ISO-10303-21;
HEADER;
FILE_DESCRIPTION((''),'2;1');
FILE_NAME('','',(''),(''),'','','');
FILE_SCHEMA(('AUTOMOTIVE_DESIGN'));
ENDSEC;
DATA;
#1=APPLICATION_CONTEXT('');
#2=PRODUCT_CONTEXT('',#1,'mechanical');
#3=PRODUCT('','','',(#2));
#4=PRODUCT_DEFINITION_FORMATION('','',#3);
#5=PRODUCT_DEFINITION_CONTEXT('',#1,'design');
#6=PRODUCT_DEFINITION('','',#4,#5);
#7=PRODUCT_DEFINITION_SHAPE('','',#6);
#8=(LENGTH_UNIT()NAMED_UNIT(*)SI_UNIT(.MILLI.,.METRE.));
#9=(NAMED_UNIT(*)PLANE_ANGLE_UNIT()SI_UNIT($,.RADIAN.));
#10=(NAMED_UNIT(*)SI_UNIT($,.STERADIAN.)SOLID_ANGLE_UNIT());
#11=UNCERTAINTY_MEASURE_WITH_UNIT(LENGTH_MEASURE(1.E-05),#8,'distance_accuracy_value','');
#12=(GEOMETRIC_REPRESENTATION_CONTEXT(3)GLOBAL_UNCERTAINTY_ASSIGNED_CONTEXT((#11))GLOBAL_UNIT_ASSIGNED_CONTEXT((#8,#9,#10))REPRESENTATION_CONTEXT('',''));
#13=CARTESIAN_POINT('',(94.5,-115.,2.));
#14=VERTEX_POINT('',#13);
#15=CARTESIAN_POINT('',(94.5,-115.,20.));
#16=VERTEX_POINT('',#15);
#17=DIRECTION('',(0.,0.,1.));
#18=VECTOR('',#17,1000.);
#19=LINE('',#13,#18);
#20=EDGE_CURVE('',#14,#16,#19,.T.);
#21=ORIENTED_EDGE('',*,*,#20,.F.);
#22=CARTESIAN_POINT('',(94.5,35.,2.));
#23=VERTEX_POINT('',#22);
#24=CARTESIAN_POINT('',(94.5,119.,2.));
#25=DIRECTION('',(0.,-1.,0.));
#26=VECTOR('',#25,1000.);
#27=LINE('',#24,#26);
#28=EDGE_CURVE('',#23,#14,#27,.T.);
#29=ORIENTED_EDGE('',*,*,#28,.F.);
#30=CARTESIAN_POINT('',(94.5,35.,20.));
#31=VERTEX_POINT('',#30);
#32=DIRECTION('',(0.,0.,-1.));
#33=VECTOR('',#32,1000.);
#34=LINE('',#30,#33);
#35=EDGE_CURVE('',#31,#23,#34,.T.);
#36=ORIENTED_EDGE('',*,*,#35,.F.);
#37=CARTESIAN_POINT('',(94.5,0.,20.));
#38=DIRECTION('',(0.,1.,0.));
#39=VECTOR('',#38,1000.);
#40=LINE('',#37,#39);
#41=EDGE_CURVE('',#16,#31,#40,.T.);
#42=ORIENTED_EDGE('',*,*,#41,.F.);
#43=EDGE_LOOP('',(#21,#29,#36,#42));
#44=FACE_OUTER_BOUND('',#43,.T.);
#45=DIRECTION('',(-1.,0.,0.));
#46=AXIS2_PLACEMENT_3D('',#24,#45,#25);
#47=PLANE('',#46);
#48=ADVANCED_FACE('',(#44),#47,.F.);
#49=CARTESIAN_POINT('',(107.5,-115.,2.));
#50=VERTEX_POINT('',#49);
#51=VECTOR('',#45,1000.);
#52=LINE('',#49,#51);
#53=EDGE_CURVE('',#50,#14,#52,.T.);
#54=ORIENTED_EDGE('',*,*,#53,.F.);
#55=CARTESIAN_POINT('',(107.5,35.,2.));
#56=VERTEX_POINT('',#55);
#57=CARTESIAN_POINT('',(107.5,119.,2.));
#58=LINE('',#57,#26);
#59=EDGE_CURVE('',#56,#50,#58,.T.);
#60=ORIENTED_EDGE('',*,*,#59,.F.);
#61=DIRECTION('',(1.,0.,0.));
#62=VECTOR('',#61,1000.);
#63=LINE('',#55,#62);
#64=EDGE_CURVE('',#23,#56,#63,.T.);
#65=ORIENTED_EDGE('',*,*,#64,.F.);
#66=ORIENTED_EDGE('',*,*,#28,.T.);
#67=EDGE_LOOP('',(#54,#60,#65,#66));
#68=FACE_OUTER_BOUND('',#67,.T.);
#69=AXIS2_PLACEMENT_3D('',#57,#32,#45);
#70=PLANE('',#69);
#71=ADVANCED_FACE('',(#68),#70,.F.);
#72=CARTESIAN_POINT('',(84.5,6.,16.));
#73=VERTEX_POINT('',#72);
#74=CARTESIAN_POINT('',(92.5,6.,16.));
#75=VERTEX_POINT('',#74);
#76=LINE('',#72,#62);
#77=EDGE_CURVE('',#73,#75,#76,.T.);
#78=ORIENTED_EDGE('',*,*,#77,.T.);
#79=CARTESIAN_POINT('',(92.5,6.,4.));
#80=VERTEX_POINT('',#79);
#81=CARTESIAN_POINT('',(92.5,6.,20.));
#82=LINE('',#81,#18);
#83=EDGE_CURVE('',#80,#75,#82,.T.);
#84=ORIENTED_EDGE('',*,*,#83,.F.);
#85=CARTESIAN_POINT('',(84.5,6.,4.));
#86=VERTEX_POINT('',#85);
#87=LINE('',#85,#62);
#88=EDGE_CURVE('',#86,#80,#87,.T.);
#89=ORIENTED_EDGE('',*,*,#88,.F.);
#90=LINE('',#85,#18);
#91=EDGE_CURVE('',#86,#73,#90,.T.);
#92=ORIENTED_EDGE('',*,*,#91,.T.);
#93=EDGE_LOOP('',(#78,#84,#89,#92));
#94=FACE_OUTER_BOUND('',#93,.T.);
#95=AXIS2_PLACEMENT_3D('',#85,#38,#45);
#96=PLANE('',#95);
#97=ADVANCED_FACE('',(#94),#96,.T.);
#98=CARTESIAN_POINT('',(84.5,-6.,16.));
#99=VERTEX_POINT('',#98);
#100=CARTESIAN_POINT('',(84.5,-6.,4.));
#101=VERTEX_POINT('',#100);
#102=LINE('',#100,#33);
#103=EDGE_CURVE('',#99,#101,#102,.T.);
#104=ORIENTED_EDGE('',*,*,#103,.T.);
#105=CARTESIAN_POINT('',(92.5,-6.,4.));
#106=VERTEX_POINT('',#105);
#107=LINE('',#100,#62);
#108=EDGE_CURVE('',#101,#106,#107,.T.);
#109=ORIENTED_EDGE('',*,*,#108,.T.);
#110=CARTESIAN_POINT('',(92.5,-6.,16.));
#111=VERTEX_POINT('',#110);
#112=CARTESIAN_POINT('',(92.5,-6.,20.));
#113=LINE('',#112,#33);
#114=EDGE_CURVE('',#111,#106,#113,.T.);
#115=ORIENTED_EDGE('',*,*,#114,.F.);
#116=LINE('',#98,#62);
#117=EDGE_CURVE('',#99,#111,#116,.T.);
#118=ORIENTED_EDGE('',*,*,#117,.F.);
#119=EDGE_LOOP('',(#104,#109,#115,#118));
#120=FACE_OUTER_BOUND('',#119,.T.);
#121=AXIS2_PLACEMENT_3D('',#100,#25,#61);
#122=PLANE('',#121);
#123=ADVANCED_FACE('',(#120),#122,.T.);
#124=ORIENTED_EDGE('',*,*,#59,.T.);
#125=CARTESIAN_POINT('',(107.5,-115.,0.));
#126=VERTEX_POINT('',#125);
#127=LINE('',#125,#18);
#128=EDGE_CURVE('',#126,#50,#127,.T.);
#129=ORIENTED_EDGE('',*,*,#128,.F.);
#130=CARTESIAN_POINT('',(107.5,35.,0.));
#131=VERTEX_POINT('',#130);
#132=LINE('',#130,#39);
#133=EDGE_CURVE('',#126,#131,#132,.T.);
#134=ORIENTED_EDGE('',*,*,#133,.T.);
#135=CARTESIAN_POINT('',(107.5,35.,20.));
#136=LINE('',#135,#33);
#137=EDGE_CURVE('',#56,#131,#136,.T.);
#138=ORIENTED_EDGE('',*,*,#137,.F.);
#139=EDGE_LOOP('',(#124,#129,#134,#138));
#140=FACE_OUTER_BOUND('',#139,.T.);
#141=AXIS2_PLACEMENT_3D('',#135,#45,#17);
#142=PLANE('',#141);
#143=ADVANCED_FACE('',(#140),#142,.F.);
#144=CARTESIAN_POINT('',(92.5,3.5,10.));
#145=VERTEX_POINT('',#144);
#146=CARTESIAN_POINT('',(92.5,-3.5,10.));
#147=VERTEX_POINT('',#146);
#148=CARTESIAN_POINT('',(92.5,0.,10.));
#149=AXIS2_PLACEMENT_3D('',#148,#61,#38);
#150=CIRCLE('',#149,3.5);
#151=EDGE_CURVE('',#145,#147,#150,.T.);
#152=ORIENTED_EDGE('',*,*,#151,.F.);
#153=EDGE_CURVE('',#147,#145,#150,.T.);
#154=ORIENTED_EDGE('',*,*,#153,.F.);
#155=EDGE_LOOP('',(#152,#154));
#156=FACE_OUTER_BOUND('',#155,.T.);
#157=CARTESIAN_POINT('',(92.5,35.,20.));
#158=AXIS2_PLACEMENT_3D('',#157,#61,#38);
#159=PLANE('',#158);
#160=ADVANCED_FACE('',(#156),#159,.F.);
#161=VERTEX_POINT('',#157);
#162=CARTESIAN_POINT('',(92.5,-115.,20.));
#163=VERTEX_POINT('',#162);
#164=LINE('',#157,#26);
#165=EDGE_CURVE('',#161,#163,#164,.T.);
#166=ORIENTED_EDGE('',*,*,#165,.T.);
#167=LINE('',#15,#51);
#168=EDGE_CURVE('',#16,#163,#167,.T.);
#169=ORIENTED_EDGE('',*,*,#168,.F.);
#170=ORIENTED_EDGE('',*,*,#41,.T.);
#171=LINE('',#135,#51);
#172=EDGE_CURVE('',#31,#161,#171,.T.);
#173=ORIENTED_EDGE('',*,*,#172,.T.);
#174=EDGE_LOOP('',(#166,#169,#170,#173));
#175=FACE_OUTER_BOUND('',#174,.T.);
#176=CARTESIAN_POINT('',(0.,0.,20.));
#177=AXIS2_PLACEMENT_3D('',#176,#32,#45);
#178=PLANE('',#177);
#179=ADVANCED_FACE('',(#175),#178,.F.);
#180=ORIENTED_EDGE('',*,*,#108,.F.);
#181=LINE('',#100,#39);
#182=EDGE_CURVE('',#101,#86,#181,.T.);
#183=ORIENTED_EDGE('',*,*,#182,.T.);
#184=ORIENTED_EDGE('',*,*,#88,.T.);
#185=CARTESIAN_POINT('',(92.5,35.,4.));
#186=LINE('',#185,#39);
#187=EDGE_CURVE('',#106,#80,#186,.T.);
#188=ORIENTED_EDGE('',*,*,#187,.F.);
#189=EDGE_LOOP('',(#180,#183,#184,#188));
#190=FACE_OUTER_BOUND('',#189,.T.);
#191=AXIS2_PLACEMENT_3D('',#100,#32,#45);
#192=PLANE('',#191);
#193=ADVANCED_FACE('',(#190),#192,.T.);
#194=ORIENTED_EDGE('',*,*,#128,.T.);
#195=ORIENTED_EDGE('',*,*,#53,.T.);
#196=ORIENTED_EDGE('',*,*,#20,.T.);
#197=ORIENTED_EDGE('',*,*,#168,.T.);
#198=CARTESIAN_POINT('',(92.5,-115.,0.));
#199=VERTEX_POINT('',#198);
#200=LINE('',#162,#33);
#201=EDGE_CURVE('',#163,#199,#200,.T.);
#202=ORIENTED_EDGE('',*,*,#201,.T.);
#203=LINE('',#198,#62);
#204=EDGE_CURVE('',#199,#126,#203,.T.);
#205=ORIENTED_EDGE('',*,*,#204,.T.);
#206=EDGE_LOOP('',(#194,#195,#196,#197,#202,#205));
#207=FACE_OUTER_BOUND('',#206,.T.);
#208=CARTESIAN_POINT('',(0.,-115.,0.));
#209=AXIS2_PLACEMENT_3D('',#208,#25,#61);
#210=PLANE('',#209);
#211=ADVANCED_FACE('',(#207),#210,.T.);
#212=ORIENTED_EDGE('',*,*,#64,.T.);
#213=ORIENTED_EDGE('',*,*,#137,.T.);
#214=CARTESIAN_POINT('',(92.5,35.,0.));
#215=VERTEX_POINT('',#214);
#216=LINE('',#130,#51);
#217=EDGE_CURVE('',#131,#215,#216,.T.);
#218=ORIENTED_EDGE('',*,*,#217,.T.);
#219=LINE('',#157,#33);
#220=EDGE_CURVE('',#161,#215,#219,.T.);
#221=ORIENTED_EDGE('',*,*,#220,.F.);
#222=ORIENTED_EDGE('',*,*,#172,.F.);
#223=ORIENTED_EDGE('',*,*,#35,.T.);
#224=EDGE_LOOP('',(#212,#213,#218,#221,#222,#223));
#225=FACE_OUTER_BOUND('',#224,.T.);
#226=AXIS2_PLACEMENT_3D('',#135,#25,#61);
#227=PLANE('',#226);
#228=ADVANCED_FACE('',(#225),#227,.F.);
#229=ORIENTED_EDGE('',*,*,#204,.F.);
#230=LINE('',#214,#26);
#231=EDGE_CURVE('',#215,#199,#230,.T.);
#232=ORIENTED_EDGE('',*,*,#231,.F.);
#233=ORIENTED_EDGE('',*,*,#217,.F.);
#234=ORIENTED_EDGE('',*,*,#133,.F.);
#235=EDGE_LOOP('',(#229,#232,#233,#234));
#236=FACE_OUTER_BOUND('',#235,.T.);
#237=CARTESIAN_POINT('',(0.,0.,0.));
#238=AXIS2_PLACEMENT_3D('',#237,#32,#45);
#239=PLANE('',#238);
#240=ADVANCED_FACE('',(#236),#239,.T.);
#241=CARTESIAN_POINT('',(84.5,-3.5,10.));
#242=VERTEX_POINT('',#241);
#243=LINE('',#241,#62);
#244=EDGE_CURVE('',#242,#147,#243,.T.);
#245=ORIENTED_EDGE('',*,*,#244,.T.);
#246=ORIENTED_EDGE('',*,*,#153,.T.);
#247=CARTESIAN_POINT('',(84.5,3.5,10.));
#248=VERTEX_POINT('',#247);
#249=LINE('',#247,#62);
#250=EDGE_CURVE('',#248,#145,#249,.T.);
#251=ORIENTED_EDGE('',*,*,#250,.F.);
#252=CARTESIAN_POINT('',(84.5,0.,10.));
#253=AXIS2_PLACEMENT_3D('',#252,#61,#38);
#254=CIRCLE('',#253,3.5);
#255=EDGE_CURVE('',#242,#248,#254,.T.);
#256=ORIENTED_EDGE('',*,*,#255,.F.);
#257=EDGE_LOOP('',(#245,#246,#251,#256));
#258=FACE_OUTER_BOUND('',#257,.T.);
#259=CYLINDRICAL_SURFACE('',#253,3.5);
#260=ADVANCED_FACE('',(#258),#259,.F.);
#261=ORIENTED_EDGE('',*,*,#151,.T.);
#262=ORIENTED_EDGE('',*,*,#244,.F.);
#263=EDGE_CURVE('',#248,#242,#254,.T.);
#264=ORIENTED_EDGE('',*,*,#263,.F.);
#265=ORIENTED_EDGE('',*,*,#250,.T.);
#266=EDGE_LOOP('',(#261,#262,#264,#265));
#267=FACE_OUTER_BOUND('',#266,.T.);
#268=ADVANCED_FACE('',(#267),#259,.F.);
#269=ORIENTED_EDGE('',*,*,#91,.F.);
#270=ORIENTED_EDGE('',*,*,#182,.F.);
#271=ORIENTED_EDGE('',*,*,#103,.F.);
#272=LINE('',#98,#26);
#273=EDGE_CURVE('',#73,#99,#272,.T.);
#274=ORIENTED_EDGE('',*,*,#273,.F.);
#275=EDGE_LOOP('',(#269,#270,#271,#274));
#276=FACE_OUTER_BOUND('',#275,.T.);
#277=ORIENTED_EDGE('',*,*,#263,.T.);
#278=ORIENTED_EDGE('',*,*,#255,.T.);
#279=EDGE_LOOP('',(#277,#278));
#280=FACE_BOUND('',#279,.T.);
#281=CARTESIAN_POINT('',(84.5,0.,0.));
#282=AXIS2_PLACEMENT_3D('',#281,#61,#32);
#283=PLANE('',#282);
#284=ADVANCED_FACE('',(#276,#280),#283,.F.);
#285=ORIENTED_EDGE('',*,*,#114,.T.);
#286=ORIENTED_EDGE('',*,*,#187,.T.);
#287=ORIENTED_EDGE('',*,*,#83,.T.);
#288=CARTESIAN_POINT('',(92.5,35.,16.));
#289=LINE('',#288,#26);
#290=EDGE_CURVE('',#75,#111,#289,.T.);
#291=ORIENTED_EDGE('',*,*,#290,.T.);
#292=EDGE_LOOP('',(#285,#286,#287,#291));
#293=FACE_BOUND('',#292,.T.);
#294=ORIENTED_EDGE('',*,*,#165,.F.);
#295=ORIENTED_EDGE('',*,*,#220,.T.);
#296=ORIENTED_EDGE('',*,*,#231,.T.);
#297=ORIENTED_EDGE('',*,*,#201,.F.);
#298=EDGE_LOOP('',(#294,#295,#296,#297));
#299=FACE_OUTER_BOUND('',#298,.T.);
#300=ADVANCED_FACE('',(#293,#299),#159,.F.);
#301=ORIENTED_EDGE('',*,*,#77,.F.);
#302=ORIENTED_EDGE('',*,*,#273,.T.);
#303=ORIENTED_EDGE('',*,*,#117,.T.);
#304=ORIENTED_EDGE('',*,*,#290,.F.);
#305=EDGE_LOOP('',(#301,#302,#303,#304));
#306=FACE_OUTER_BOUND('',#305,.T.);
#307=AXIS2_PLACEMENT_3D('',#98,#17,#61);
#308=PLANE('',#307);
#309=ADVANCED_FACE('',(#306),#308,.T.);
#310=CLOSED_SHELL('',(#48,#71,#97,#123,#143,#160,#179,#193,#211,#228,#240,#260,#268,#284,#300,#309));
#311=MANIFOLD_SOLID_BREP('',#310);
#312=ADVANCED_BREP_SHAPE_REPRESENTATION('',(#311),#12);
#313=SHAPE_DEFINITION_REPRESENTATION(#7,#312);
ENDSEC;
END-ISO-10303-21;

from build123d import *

# Parameters (mm, degrees)
SKETCH1_W           = 15
SKETCH1_H           = 70
BOSS_EXTRUDE1_DEPTH = 20
SKETCH2_W           = 13
SKETCH2_H           = 18
CUT_EXTRUDE1_DEPTH  = 154
BOSS_EXTRUDE2_DEPTH = 80
SKETCH4_W           = 12
SKETCH4_H           = 12
SKETCH4_R           = 3.5
BOSS_EXTRUDE4_DEPTH = 10


with BuildPart() as part:
    # Sketch1 → Boss-Extrude1 (new body)
    with BuildSketch(Plane.XY):
        with Locations((100, 0)):
            Rectangle(SKETCH1_W, SKETCH1_H)
    extrude(amount=BOSS_EXTRUDE1_DEPTH)

    # Sketch2 → Cut-Extrude1 (cut)
    with BuildSketch(Plane(origin=(0, -35, 0), x_dir=(-1, 0, 0), z_dir=(0, -1, 0))):
        with Locations((-101, -11)):
            Rectangle(SKETCH2_W, SKETCH2_H)
    extrude(amount=-CUT_EXTRUDE1_DEPTH, mode=Mode.SUBTRACT)

    # Sketch3 → Boss-Extrude2 (add)
    with BuildSketch(Plane.XZ.offset(35)):
        Polygon((107.5, 0), (107.5, 2), (94.5, 2), (94.5, 20), (92.5, 20), (92.5, 0), align=None)
    extrude(amount=BOSS_EXTRUDE2_DEPTH)

    # Sketch4 → Boss-Extrude4 (add)
    with BuildSketch(Plane(origin=(94.5, 0, 0), x_dir=(0, 0, -1), z_dir=(1, 0, 0))):
        with Locations((-10, 0)):
            Rectangle(SKETCH4_W, SKETCH4_H)
        with Locations(Location((-10, 0, 0), (0, 0, 90))):
            Circle(SKETCH4_R, mode=Mode.SUBTRACT)
    extrude(amount=-BOSS_EXTRUDE4_DEPTH)


solid = part.part
